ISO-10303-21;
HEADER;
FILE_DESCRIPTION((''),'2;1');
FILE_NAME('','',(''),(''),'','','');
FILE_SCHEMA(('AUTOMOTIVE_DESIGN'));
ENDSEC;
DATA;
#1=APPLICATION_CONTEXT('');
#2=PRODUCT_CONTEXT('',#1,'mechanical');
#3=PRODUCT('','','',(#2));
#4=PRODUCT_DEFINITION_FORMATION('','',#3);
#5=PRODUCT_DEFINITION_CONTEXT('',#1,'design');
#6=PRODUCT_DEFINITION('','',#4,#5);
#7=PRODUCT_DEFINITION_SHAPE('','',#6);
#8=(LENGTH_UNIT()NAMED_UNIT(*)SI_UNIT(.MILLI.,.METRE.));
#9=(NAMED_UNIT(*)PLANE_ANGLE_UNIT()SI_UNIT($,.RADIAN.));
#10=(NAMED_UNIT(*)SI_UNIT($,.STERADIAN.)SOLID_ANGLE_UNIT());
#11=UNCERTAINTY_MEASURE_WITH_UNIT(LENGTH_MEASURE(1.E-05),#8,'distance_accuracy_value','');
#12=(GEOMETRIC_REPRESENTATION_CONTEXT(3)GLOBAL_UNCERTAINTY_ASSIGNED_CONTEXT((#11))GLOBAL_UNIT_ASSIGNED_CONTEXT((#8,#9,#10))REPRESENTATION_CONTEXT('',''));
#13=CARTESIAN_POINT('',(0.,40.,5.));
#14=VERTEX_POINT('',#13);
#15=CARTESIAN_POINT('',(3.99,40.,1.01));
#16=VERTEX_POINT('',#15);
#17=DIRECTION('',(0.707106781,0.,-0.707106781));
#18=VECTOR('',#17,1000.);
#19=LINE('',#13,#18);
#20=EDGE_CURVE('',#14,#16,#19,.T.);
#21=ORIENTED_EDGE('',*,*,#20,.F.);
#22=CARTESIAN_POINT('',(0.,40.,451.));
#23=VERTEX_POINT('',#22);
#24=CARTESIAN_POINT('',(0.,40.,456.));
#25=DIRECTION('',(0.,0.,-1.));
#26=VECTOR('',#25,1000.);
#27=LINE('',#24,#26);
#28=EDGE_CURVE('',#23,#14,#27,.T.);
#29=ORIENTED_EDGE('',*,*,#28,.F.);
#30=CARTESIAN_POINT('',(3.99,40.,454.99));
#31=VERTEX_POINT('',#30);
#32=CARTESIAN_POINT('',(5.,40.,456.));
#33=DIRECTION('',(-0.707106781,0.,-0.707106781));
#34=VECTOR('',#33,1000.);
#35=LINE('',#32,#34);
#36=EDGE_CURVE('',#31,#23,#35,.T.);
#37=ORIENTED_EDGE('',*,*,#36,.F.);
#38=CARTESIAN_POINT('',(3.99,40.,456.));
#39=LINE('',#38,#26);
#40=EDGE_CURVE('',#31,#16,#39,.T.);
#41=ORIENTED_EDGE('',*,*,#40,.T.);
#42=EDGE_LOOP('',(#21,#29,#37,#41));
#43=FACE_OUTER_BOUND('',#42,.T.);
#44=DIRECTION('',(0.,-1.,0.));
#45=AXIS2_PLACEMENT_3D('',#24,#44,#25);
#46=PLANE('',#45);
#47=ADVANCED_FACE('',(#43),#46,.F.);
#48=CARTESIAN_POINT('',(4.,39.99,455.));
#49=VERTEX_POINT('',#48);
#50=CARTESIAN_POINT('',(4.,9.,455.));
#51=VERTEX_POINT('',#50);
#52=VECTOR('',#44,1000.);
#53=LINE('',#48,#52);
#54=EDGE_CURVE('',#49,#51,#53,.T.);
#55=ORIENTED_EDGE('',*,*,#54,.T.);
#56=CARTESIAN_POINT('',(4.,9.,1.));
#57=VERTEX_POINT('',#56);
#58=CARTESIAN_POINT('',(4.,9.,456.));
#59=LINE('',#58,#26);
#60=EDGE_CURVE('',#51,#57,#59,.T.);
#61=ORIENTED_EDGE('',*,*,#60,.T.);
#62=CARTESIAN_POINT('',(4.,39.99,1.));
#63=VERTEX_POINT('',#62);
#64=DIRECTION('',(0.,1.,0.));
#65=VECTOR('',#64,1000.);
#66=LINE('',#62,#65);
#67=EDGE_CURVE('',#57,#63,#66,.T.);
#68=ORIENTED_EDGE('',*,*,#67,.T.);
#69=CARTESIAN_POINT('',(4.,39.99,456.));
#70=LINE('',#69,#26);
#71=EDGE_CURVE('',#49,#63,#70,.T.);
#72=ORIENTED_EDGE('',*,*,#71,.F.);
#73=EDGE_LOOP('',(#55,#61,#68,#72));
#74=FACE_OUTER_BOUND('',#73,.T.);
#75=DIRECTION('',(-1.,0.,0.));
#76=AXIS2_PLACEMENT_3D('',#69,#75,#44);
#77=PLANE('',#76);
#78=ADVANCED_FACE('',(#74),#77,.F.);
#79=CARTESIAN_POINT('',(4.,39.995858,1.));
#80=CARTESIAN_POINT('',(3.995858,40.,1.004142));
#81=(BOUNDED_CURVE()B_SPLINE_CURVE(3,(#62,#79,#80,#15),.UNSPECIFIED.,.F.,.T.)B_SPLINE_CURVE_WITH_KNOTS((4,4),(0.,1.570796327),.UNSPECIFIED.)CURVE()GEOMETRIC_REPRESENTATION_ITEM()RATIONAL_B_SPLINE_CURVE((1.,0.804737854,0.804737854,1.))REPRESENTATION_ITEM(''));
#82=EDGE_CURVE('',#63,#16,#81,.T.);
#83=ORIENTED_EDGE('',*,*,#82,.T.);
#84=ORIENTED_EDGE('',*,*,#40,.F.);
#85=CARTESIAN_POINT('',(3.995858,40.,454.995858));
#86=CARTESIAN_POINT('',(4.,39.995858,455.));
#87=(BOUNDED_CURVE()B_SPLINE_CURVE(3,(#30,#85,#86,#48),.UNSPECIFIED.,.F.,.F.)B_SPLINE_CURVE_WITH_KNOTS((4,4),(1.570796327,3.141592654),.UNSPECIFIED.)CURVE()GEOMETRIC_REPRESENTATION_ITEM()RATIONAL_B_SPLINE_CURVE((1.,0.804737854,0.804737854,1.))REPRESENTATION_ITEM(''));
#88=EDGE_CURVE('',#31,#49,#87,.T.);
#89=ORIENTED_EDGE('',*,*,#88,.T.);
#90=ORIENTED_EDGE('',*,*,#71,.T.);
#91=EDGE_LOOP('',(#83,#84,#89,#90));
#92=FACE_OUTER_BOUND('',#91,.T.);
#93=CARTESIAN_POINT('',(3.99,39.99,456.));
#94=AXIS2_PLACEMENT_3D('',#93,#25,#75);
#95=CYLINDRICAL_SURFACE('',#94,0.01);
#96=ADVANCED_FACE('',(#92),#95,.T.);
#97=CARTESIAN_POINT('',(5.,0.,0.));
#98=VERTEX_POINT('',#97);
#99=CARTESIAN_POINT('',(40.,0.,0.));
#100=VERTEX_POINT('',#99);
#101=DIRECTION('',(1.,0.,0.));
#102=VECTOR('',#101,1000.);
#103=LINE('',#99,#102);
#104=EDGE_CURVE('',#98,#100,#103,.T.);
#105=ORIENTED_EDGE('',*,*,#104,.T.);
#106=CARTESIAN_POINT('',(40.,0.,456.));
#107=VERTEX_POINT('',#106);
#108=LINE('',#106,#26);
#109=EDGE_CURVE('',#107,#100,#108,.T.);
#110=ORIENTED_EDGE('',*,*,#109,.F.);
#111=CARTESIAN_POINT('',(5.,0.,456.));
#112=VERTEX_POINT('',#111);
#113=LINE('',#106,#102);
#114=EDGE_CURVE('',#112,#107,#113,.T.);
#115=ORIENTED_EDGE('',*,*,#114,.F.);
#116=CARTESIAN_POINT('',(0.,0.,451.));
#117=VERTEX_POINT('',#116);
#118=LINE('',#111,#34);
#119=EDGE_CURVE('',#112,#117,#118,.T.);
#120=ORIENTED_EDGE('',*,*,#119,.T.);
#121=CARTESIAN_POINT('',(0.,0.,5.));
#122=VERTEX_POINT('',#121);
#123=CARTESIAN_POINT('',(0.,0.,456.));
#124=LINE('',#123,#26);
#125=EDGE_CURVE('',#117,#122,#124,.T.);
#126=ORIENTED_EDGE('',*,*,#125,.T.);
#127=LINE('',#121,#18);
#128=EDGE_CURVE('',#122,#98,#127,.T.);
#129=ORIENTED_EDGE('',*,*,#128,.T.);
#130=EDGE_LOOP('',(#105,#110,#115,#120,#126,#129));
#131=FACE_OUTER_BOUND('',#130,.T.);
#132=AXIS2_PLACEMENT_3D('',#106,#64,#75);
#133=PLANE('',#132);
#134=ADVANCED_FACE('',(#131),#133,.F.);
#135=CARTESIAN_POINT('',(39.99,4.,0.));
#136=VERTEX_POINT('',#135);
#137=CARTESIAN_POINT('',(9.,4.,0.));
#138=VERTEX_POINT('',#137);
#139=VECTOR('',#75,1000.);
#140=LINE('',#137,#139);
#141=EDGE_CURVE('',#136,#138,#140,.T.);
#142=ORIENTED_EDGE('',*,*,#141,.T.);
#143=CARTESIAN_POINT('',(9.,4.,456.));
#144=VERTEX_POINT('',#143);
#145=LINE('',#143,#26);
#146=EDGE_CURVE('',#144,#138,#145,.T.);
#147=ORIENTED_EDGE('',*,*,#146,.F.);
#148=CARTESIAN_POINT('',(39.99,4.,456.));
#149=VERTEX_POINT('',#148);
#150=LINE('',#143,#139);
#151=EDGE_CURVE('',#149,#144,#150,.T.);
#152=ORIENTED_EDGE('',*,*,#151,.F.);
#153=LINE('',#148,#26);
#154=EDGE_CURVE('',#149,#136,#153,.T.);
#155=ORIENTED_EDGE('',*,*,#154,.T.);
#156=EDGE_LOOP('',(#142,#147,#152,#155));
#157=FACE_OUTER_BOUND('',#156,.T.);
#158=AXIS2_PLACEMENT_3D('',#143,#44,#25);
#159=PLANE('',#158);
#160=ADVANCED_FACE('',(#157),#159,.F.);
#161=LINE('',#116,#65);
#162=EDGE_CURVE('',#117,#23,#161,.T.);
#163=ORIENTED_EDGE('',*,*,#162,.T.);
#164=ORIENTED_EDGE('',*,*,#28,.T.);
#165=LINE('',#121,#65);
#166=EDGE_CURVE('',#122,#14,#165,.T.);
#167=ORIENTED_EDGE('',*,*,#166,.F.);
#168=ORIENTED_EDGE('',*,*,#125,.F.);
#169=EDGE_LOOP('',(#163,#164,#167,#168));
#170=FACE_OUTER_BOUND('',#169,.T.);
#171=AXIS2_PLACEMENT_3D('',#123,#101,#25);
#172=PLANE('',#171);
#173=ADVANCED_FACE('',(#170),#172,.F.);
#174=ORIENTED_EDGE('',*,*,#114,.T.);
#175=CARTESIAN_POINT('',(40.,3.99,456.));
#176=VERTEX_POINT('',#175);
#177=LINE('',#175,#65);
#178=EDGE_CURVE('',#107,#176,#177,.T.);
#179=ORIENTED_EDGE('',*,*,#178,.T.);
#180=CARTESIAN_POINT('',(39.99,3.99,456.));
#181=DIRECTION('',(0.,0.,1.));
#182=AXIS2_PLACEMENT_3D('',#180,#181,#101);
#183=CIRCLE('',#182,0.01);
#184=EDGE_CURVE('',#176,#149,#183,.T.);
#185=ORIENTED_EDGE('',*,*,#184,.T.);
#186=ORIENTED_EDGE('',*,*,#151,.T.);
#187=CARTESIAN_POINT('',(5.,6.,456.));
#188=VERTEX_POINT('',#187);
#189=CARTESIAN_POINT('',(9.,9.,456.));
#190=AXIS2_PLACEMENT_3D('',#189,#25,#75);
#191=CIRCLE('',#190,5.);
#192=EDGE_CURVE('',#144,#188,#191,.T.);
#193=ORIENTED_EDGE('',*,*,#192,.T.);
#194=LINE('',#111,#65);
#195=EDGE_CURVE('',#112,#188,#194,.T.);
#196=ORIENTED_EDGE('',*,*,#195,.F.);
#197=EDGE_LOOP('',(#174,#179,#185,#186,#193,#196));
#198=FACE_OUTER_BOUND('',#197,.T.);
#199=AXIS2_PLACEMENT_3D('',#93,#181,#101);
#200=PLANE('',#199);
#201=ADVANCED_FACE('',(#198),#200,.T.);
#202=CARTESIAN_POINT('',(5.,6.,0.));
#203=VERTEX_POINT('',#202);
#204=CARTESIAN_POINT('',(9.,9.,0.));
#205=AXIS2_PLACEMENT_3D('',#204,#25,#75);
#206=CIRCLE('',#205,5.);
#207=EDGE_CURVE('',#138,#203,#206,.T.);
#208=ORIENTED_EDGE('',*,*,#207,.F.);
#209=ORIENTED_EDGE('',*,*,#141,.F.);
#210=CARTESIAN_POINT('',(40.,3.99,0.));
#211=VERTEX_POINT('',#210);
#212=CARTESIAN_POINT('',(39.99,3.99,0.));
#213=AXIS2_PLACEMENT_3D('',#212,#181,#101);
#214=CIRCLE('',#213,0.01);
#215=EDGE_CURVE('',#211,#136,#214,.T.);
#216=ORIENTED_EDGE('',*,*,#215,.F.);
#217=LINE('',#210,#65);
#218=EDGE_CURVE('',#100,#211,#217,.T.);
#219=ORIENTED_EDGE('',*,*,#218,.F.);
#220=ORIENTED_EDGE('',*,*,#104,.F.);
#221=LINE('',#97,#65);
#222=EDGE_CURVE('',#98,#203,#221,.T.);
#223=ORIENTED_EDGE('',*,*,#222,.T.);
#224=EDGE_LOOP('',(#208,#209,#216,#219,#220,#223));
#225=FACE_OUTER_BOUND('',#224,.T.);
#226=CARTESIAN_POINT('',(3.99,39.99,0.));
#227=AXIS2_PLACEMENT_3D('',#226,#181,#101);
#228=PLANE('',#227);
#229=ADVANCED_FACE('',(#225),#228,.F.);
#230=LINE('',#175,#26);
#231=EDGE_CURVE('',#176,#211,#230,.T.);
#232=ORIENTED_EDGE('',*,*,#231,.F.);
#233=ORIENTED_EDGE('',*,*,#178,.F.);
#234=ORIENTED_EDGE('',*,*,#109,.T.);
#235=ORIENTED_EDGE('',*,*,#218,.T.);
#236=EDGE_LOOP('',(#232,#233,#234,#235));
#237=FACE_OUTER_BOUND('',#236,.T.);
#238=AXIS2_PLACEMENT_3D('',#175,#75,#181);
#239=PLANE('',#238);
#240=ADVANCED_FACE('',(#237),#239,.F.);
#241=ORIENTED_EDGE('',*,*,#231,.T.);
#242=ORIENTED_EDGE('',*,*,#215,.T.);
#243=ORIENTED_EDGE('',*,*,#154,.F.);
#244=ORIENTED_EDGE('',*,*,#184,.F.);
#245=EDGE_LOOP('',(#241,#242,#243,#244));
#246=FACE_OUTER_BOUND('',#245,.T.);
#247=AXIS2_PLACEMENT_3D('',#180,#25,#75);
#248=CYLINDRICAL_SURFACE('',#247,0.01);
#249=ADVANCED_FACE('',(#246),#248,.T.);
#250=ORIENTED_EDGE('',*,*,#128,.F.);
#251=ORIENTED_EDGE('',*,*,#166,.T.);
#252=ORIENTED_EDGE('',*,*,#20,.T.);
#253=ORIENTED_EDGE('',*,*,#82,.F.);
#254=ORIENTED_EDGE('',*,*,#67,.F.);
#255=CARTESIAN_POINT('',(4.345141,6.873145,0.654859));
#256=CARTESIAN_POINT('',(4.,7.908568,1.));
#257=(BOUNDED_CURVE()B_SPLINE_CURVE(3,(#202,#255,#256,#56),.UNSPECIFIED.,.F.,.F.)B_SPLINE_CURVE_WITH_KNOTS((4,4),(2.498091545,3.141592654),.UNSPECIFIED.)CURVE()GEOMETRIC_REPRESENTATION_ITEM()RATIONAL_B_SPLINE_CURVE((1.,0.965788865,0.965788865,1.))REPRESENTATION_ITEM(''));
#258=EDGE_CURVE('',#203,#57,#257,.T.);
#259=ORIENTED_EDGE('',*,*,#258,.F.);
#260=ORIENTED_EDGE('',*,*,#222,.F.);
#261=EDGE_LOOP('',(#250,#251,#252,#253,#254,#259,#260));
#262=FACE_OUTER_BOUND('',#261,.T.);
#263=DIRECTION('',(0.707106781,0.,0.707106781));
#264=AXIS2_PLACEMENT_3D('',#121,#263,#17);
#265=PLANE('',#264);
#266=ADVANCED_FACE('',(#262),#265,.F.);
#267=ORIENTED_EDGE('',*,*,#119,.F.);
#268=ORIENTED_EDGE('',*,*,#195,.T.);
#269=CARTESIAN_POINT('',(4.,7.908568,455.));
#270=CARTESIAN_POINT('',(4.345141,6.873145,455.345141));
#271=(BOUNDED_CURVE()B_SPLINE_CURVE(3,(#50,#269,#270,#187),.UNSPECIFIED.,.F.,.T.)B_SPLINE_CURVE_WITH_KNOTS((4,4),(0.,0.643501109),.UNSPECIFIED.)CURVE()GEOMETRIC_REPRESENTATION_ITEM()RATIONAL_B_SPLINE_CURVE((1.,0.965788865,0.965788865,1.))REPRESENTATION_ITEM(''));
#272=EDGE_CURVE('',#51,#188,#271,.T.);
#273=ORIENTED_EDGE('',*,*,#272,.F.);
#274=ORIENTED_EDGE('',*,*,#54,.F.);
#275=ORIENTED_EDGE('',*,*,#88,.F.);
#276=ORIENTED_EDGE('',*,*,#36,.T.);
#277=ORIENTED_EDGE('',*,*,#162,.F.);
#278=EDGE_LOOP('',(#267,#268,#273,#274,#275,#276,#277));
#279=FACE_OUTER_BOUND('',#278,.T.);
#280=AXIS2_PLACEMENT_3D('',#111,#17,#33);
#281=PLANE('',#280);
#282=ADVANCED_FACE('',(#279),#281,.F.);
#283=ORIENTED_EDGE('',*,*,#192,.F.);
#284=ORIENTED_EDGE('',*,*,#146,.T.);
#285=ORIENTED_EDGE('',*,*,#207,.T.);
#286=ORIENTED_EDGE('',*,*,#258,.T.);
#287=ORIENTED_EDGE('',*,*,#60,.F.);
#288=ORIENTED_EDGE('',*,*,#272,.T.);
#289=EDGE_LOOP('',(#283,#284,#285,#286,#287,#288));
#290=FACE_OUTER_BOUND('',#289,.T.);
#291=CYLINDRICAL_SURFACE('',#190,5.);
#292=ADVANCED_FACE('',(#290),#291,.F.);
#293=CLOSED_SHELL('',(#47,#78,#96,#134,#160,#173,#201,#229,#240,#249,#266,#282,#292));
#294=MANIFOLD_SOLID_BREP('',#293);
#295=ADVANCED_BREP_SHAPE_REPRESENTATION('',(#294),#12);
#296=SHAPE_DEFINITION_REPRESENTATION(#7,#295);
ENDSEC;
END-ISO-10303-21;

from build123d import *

# Parameters (mm, degrees)
EXTRUDE_1_DEPTH     = 456
CUT_EXTRUDE_1_DEPTH = 40


with BuildPart() as part:
    # 草图1 → 拉伸1 (new body)
    with BuildSketch(Plane.XY):
        with BuildLine():
            Line((0, 0), (0, 40))
            Line((0, 40), (3.99, 40))
            ThreePointArc((3.99, 40), (3.997071068, 39.997071068), (4, 39.99))
            Line((4, 39.99), (4, 9))
            ThreePointArc((4, 9), (5.464466094, 5.464466094), (9, 4))
            Line((9, 4), (39.99, 4))
            ThreePointArc((39.99, 4), (39.997071068, 3.997071068), (40, 3.99))
            Line((40, 3.99), (40, 0))
            Line((40, 0), (0, 0))
        make_face()
    extrude(amount=EXTRUDE_1_DEPTH)

    # 草图2 → 切除-拉伸1 (cut)
    with BuildSketch(Plane(origin=(0, 40, 0), x_dir=(1, 0, 0), z_dir=(0, 1, 0))):
        Polygon((5, -456), (0, -451), (0, -456), align=None)
        Polygon((0, 0), (0, -5), (5, 0), align=None)
    extrude(amount=-CUT_EXTRUDE_1_DEPTH, mode=Mode.SUBTRACT)


solid = part.part
